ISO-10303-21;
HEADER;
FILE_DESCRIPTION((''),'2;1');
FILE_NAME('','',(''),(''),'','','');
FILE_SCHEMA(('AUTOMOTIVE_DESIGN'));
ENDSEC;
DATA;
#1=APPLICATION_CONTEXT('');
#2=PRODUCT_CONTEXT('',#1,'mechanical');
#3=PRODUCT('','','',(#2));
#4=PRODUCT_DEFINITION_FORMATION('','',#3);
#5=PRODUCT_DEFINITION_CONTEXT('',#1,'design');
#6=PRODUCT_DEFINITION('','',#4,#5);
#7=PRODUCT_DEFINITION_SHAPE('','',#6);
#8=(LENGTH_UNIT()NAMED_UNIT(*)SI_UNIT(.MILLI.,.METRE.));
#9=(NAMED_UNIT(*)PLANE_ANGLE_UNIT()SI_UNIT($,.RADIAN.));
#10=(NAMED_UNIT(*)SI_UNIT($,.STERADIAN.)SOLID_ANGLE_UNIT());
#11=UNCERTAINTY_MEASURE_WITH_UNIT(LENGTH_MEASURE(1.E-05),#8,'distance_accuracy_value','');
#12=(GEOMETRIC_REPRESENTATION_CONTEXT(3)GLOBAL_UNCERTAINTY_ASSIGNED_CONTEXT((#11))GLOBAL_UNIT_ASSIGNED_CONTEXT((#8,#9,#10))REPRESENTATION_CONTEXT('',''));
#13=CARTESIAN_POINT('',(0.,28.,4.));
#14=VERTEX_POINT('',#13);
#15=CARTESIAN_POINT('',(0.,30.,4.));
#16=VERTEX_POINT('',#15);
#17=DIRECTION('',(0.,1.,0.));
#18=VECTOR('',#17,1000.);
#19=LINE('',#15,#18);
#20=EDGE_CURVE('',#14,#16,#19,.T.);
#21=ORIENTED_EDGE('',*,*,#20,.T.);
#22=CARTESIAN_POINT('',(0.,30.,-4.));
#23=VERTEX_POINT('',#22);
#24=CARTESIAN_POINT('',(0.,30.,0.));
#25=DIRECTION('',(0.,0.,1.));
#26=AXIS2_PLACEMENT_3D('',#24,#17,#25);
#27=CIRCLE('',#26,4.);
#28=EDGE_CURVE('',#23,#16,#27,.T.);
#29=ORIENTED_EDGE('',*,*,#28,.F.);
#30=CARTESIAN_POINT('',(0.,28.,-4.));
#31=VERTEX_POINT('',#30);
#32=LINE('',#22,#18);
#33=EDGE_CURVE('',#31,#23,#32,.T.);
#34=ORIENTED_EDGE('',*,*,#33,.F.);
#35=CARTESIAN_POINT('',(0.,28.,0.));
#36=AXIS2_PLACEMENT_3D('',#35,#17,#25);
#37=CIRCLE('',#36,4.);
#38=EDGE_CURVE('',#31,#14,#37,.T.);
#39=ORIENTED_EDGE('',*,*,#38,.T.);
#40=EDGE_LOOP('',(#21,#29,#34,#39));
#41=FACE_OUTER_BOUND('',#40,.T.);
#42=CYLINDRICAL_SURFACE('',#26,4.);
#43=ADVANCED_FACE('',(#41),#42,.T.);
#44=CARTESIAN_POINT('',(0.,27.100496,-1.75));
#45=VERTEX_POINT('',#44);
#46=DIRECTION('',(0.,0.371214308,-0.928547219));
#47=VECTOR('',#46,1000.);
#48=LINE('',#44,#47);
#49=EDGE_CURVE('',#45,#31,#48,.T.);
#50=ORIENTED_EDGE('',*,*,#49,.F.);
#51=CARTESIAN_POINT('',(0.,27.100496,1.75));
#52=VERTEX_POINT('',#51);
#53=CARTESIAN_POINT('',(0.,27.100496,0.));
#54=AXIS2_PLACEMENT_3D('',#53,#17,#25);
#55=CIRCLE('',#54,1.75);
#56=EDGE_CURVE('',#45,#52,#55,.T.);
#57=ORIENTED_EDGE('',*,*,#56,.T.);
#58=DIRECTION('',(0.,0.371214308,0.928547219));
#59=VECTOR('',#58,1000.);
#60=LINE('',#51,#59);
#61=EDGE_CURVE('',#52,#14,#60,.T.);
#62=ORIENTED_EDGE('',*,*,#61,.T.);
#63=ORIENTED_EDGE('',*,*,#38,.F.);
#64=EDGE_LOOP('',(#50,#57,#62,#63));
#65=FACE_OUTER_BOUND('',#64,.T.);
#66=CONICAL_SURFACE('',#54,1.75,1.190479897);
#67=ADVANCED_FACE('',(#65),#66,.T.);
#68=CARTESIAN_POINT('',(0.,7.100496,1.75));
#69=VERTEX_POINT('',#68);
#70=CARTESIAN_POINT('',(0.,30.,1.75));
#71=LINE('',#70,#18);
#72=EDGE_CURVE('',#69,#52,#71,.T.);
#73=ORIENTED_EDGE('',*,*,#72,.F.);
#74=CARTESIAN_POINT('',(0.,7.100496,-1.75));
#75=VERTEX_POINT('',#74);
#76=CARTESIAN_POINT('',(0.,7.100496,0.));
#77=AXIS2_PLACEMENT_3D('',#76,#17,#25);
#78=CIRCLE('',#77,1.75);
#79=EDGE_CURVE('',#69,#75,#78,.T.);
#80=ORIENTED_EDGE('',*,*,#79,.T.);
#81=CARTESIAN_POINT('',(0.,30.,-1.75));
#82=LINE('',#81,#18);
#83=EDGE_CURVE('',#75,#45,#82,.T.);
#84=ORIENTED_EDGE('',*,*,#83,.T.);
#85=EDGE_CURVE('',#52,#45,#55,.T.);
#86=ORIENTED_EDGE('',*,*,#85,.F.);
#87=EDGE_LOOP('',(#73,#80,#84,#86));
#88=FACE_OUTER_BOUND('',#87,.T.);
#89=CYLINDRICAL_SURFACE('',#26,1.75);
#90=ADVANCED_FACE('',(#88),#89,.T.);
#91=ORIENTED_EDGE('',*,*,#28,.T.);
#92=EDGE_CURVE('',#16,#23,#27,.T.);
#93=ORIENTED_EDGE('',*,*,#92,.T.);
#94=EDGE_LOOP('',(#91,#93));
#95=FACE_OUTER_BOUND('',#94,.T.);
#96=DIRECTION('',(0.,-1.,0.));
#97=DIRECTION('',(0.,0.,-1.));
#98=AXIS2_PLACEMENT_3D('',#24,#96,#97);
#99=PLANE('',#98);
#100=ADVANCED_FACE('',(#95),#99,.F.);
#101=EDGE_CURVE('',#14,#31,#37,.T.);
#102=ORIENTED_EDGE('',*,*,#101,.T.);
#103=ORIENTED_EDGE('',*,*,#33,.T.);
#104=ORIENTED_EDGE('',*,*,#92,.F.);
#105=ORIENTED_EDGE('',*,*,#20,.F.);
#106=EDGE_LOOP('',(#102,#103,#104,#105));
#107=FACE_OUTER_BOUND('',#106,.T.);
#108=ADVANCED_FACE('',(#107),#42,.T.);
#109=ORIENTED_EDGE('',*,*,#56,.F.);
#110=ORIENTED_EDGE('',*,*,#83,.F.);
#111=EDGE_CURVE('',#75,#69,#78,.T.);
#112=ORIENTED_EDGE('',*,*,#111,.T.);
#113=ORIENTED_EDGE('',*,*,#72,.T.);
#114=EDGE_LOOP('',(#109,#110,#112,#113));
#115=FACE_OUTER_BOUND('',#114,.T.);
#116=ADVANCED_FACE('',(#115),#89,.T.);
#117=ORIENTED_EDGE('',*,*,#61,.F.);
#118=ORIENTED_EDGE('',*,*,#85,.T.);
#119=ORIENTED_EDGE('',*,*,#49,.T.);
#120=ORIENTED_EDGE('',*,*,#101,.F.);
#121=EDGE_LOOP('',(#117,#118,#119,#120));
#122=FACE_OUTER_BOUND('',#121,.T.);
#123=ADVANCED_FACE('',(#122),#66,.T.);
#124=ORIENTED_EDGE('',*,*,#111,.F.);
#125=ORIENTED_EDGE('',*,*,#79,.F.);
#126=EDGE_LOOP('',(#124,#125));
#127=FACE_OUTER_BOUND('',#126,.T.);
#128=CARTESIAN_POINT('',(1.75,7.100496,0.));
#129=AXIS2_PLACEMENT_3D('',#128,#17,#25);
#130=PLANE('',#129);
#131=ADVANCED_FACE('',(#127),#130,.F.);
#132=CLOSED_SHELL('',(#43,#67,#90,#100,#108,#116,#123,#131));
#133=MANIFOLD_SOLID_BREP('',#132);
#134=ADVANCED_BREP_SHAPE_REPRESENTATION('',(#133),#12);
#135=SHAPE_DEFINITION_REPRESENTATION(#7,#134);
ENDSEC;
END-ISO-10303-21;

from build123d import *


with BuildPart() as part:
    # Sketch1 → Revolve1 (revolve)
    with BuildSketch(Plane.XY, mode=Mode.PRIVATE) as revolve1_sk:
        Polygon((0, 30), (4, 30), (4, 28), (1.75, 27.100495725), (1.75, 7.100495725), (0, 7.100495725), align=None)
    revolve(revolve1_sk.sketch.rotate(Axis((0, 30, 0), (0, -1, 0)), 90), axis=Axis((0, 30, 0), (0, -1, 0)))


solid = part.part
